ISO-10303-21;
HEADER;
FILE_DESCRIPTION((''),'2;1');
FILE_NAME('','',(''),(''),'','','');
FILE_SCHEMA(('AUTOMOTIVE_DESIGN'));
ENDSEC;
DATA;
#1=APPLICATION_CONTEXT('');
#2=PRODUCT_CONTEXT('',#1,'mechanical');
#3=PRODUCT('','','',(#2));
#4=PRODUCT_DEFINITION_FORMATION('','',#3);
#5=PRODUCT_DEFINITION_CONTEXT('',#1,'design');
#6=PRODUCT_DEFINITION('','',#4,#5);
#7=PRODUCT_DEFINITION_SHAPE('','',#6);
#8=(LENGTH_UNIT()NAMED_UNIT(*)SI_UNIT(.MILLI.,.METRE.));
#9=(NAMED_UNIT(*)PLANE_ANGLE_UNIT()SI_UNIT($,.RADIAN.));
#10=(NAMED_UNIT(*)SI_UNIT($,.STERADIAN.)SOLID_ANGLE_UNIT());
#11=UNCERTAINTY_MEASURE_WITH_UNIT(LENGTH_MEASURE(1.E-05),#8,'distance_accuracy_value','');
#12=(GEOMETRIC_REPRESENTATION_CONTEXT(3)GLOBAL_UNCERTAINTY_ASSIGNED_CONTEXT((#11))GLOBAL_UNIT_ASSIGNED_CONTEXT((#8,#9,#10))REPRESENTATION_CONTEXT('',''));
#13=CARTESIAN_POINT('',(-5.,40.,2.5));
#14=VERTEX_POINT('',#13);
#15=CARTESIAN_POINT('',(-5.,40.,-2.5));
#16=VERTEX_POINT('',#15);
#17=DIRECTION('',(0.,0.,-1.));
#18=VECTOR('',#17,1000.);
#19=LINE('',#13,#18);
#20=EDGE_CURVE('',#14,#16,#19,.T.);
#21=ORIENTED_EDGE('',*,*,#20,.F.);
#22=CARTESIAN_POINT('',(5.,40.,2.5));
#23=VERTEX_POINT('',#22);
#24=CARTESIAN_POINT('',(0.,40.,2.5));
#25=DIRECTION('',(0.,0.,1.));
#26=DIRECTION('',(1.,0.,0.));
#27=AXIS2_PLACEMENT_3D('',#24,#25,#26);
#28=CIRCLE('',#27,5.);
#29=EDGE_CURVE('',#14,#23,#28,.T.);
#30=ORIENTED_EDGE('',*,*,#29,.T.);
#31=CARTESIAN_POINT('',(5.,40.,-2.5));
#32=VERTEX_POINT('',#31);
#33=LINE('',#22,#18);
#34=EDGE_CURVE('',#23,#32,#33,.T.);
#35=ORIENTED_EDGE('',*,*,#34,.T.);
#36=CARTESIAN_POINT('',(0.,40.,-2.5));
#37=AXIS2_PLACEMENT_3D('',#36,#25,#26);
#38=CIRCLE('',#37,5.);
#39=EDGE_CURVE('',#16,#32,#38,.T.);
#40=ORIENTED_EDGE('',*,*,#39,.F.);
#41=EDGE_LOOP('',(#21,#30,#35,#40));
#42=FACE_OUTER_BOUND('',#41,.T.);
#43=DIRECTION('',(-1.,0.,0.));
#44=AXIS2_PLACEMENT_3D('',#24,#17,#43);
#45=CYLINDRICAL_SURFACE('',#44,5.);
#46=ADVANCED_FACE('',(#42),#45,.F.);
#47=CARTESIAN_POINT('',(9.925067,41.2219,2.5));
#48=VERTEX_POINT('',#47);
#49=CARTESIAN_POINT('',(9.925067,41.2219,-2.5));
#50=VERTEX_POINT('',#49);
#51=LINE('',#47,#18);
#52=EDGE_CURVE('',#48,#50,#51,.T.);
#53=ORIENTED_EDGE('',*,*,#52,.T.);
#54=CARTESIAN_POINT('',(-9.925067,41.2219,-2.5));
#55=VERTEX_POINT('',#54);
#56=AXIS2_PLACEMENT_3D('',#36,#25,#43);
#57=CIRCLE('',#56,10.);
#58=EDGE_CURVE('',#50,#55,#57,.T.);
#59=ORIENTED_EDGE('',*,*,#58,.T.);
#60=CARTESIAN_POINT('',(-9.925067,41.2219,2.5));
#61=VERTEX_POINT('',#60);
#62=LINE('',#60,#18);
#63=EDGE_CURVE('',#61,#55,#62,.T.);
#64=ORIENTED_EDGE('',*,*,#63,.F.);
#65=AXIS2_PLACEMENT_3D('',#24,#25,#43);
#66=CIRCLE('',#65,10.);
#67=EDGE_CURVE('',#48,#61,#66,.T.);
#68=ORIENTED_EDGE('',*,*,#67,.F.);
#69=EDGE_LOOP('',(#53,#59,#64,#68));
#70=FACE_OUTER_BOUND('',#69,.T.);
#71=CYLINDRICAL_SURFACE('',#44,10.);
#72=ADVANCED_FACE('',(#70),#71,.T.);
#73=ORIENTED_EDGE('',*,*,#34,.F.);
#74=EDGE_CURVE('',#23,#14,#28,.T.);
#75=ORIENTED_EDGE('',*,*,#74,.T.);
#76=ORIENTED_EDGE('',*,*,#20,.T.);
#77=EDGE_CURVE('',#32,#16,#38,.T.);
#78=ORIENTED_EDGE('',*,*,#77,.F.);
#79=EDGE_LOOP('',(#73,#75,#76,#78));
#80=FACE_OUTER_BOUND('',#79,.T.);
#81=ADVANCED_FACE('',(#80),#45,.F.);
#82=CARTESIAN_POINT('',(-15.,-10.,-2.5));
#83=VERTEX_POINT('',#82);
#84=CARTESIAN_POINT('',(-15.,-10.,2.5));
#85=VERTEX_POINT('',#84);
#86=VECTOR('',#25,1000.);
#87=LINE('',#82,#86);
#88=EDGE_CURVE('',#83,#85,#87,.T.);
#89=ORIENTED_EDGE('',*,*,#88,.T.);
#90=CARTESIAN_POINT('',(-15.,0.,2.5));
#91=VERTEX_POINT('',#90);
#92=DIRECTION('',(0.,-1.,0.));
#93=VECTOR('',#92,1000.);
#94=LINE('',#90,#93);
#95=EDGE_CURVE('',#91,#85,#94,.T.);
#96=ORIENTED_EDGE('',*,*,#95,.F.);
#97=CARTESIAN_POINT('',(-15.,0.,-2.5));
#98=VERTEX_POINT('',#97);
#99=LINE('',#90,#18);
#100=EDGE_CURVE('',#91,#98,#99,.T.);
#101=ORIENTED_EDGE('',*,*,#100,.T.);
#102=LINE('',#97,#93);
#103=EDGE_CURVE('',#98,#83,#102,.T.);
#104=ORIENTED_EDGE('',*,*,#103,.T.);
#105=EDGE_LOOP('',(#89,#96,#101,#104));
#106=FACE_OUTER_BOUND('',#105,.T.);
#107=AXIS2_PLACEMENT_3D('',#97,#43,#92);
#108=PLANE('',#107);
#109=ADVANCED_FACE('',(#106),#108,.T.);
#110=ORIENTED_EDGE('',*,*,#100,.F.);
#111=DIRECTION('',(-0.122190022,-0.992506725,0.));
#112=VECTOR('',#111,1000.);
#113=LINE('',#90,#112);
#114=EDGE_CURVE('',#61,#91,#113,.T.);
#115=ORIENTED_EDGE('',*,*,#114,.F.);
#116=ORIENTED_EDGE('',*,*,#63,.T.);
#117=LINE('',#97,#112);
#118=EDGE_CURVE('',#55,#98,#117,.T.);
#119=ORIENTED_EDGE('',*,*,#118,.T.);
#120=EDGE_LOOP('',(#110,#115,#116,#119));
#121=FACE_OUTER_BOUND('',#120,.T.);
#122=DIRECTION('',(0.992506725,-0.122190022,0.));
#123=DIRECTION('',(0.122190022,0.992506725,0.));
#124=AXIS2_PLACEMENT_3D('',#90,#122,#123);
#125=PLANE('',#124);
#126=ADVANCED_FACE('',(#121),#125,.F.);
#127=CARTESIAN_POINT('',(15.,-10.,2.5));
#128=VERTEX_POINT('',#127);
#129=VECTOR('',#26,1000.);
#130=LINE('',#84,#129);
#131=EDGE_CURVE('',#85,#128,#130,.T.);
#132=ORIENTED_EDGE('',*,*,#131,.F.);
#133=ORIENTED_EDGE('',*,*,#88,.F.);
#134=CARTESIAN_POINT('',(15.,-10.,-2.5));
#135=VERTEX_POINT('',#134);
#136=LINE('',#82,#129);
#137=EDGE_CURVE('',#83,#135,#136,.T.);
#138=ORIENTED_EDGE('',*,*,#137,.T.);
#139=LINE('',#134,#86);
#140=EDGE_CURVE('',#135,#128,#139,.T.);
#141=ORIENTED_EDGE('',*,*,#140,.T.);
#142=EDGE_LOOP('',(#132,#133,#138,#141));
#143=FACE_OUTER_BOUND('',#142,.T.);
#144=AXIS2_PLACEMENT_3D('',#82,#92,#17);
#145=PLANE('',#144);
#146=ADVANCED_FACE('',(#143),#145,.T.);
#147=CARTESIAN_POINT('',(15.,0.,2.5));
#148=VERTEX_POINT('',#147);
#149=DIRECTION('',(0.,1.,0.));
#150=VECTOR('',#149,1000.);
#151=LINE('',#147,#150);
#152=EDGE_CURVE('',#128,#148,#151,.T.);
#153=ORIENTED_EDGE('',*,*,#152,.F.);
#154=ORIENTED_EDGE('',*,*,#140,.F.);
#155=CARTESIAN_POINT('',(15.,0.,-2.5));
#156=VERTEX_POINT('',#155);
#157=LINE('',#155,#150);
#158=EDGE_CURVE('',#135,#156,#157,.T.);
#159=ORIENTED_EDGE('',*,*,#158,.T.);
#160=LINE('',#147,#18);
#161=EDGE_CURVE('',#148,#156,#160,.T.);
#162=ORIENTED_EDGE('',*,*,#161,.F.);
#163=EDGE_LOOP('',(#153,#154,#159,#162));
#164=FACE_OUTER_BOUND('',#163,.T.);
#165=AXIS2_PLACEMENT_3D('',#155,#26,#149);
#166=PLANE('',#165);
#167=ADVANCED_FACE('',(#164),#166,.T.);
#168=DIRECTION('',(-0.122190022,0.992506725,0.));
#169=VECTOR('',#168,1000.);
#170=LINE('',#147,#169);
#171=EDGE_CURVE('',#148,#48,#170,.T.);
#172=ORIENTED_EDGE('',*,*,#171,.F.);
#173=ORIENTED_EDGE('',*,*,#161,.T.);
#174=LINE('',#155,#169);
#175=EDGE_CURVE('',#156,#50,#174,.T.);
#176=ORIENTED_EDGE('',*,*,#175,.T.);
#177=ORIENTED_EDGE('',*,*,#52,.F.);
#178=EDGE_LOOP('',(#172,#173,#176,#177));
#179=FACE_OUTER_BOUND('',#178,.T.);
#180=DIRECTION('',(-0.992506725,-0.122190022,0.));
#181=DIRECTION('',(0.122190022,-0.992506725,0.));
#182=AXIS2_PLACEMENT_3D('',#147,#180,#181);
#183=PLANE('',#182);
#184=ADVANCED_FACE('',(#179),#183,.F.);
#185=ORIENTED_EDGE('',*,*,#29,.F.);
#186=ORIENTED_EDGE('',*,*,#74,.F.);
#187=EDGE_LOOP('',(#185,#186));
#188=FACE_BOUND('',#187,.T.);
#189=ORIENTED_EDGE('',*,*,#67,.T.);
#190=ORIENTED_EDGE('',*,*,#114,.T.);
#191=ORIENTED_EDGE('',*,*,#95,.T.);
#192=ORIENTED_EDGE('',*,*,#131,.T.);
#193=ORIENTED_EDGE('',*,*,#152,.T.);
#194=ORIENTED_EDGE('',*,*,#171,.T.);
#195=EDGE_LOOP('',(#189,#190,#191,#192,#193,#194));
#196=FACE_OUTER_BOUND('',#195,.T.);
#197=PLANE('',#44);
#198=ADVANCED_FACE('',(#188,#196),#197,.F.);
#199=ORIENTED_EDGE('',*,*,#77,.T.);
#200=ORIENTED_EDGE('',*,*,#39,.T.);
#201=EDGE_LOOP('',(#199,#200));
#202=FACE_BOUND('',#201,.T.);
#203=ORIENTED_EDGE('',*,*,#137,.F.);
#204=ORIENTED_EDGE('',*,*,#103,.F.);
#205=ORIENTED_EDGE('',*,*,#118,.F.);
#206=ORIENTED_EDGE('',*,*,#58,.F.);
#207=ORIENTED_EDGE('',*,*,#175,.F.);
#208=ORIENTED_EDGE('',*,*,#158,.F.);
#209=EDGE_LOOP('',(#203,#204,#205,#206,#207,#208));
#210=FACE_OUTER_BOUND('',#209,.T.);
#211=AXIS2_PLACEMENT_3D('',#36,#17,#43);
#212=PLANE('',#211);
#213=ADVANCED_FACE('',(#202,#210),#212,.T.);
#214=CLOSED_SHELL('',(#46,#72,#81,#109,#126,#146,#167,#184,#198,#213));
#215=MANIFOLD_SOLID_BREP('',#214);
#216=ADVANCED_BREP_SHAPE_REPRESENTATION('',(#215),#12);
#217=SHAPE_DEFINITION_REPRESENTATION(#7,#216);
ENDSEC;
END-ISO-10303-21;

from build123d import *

# Parameters (mm, degrees)
SKETCH1_R           = 5
BOSS_EXTRUDE1_DEPTH = 2.5
SKETCH2_W           = 30
SKETCH2_H           = 10
BOSS_EXTRUDE2_DEPTH = 5


with BuildPart() as part:
    # Sketch1 → Boss-Extrude1 (new, symmetric)
    with BuildSketch(Plane.XY):
        with BuildLine():
            Line((15, 0), (-15, 0))
            Line((-15, 0), (-9.925067247, 41.221900218))
            ThreePointArc((-9.925067247, 41.221900218), (0, 50), (9.925067247, 41.221900218))
            Line((9.925067247, 41.221900218), (15, 0))
        make_face()
        with Locations((0, 40)):
            Circle(SKETCH1_R, mode=Mode.SUBTRACT)
    extrude(amount=BOSS_EXTRUDE1_DEPTH, both=True)

    # Sketch2 → Boss-Extrude2 (add)
    with BuildSketch(Plane.XY.offset(2.5)):
        with Locations((0, -5)):
            Rectangle(SKETCH2_W, SKETCH2_H)
    extrude(amount=-BOSS_EXTRUDE2_DEPTH)


solid = part.part
